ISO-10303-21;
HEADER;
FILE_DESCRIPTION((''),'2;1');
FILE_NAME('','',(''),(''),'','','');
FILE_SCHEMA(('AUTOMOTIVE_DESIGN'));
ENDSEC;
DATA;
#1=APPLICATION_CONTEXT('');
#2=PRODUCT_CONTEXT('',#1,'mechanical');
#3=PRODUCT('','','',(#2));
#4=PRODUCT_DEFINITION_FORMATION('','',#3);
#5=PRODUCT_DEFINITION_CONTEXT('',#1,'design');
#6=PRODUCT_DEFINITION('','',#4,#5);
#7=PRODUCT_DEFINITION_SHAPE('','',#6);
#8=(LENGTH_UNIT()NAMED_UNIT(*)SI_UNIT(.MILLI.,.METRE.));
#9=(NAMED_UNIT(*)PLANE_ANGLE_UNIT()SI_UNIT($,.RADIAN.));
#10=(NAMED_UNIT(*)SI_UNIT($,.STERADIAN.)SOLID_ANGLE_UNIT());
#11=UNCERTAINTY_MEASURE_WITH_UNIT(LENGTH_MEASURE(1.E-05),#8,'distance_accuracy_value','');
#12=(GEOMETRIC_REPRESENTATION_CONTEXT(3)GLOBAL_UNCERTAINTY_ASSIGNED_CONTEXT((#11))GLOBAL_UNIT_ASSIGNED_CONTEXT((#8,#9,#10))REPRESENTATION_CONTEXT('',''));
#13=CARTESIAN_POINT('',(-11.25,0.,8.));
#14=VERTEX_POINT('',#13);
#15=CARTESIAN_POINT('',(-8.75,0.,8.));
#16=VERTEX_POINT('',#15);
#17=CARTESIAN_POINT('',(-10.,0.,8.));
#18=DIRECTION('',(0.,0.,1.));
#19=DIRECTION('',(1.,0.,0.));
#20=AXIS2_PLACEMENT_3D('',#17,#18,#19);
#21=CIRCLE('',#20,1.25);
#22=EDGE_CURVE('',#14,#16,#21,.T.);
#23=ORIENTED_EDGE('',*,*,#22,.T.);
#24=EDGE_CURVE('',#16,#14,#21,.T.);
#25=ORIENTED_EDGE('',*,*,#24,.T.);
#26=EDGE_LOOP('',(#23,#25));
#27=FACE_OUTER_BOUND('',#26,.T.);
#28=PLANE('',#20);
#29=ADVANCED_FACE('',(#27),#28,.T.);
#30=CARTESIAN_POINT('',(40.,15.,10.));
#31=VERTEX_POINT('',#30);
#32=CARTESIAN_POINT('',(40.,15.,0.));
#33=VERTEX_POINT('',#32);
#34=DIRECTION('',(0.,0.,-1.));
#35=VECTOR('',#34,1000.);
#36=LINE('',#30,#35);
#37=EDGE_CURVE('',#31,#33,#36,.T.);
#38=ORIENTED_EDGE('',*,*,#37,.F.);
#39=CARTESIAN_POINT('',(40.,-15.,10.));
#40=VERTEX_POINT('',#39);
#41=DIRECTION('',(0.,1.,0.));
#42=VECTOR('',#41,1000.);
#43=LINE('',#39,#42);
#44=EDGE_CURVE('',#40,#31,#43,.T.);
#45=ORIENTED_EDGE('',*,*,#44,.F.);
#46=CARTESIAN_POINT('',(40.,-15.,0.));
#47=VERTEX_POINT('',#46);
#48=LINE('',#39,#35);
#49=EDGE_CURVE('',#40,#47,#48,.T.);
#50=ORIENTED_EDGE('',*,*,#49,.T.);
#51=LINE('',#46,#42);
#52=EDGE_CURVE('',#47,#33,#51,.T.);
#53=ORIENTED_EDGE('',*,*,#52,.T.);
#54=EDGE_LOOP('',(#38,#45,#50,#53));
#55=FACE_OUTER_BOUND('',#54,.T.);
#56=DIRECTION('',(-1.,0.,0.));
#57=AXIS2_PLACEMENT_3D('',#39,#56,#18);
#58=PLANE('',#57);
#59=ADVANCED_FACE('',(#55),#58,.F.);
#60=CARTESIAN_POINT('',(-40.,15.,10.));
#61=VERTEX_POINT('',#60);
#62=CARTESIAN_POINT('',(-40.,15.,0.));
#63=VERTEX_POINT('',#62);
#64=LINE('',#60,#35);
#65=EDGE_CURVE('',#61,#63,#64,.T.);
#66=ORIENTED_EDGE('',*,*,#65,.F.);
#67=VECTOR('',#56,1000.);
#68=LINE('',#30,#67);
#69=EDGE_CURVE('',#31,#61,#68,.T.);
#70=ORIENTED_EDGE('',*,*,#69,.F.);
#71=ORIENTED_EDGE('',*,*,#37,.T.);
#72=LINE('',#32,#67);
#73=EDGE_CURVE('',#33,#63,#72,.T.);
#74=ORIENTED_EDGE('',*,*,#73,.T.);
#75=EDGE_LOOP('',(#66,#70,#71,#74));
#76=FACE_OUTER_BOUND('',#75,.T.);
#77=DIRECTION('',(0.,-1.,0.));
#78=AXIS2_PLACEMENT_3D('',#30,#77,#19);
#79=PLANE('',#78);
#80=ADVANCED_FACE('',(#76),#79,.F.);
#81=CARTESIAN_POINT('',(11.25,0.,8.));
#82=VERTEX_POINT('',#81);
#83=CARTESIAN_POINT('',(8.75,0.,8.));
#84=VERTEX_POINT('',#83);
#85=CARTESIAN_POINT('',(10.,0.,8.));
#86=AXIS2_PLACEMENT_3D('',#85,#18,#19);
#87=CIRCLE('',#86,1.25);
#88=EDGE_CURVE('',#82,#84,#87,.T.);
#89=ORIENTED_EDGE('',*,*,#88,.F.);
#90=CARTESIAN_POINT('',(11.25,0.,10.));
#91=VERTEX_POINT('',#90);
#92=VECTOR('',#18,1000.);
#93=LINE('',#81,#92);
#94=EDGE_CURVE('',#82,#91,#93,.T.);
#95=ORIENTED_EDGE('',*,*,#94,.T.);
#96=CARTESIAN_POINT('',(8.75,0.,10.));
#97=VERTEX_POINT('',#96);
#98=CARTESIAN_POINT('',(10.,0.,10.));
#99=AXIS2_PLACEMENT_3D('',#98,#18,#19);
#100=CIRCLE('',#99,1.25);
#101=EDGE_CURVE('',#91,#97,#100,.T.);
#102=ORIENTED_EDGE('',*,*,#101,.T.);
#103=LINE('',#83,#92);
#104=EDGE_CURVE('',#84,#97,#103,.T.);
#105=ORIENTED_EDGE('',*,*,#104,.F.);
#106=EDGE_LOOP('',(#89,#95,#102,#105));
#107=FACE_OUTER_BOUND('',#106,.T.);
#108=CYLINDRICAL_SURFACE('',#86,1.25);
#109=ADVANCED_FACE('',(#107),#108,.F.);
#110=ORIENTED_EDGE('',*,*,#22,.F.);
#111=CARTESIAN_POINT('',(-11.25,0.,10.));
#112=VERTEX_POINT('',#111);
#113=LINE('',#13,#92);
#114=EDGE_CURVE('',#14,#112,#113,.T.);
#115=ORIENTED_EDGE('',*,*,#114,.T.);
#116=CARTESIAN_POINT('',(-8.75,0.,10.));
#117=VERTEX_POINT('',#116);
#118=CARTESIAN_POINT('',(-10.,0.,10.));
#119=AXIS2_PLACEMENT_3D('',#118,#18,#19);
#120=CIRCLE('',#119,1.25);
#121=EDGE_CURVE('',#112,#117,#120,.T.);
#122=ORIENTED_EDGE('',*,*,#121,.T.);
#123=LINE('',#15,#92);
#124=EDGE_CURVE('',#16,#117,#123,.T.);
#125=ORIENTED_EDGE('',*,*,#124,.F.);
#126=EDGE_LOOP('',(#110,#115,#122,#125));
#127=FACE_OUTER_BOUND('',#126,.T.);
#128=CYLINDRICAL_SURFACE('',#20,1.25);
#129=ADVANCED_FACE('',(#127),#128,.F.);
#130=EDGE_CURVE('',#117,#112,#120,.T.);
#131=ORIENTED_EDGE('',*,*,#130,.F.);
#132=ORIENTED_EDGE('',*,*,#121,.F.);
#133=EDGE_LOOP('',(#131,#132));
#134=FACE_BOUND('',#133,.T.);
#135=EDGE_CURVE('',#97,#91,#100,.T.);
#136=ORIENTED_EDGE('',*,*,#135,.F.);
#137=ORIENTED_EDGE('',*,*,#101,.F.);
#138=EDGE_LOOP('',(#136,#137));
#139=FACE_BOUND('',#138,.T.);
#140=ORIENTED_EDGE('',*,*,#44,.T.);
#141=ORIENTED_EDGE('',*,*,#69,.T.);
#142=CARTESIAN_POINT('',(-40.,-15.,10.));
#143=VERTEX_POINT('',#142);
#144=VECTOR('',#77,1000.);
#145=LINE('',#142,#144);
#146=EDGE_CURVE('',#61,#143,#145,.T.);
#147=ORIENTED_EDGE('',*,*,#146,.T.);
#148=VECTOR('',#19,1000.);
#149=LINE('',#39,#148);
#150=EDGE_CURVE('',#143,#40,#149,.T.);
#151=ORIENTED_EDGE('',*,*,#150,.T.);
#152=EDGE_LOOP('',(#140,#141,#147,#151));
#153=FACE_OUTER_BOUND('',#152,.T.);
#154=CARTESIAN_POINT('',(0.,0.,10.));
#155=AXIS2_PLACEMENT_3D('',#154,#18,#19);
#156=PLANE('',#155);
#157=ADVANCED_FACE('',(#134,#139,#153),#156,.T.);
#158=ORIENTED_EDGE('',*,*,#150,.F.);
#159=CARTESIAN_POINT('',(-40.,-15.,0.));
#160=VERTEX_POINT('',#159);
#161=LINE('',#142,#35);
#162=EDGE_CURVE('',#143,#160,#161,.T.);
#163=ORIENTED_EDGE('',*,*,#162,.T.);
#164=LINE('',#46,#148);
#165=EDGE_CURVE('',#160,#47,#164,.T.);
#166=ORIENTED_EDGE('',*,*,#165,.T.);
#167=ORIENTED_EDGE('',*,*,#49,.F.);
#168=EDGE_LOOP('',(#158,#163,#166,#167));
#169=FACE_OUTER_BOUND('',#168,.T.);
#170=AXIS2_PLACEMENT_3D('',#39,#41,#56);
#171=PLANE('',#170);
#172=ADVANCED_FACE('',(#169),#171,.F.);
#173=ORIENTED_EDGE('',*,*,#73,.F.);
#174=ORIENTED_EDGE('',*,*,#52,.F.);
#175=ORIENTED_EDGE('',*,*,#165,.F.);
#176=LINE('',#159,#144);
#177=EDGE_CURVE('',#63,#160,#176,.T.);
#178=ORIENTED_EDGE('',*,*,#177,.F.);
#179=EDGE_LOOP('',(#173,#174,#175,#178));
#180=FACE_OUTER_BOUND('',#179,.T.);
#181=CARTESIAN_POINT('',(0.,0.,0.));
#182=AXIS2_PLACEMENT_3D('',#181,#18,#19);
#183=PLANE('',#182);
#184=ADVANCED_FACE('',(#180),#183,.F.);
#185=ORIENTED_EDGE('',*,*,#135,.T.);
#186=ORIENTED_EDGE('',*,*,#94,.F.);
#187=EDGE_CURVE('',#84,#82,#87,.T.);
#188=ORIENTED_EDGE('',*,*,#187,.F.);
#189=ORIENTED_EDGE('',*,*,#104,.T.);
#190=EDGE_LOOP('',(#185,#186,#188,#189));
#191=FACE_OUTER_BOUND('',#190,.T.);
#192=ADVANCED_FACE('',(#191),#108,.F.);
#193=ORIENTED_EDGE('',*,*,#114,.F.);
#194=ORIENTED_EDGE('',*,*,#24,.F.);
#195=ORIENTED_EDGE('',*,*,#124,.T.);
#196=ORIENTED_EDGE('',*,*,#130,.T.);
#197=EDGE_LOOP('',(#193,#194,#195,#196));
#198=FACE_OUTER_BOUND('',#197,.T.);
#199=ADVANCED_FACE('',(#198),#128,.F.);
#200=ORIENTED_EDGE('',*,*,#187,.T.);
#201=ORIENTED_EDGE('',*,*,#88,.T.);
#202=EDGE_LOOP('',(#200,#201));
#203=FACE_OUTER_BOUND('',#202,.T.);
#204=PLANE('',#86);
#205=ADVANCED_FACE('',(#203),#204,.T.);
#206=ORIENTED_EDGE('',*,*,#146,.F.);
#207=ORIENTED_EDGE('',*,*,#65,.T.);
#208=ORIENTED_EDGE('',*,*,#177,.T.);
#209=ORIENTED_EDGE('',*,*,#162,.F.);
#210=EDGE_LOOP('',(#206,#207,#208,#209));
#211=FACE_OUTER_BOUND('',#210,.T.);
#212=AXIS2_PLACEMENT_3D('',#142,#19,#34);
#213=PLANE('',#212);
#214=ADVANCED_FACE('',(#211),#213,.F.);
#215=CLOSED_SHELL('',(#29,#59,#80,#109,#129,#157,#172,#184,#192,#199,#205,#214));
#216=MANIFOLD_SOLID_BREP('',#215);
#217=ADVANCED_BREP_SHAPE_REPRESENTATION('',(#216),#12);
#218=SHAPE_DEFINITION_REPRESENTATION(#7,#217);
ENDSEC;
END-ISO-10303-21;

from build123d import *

# Parameters (mm, degrees)
SKETCH_1_W          = 80
SKETCH_1_H          = 30
EXTRUDE_1_DEPTH     = 10
SKETCH_2_R          = 1.25
CUT_EXTRUDE_1_DEPTH = 2


with BuildPart() as part:
    # 草图1 → 凸台-拉伸1 (new body)
    with BuildSketch(Plane.XY):
        Rectangle(SKETCH_1_W, SKETCH_1_H)
    extrude(amount=EXTRUDE_1_DEPTH)

    # 草图2 → 切除-拉伸1 (cut)
    with BuildSketch(Plane.XY.offset(10)):
        with Locations((-10, 0)):
            Circle(SKETCH_2_R)
        with Locations((10, 0)):
            Circle(SKETCH_2_R)
    extrude(amount=-CUT_EXTRUDE_1_DEPTH, mode=Mode.SUBTRACT)


solid = part.part
